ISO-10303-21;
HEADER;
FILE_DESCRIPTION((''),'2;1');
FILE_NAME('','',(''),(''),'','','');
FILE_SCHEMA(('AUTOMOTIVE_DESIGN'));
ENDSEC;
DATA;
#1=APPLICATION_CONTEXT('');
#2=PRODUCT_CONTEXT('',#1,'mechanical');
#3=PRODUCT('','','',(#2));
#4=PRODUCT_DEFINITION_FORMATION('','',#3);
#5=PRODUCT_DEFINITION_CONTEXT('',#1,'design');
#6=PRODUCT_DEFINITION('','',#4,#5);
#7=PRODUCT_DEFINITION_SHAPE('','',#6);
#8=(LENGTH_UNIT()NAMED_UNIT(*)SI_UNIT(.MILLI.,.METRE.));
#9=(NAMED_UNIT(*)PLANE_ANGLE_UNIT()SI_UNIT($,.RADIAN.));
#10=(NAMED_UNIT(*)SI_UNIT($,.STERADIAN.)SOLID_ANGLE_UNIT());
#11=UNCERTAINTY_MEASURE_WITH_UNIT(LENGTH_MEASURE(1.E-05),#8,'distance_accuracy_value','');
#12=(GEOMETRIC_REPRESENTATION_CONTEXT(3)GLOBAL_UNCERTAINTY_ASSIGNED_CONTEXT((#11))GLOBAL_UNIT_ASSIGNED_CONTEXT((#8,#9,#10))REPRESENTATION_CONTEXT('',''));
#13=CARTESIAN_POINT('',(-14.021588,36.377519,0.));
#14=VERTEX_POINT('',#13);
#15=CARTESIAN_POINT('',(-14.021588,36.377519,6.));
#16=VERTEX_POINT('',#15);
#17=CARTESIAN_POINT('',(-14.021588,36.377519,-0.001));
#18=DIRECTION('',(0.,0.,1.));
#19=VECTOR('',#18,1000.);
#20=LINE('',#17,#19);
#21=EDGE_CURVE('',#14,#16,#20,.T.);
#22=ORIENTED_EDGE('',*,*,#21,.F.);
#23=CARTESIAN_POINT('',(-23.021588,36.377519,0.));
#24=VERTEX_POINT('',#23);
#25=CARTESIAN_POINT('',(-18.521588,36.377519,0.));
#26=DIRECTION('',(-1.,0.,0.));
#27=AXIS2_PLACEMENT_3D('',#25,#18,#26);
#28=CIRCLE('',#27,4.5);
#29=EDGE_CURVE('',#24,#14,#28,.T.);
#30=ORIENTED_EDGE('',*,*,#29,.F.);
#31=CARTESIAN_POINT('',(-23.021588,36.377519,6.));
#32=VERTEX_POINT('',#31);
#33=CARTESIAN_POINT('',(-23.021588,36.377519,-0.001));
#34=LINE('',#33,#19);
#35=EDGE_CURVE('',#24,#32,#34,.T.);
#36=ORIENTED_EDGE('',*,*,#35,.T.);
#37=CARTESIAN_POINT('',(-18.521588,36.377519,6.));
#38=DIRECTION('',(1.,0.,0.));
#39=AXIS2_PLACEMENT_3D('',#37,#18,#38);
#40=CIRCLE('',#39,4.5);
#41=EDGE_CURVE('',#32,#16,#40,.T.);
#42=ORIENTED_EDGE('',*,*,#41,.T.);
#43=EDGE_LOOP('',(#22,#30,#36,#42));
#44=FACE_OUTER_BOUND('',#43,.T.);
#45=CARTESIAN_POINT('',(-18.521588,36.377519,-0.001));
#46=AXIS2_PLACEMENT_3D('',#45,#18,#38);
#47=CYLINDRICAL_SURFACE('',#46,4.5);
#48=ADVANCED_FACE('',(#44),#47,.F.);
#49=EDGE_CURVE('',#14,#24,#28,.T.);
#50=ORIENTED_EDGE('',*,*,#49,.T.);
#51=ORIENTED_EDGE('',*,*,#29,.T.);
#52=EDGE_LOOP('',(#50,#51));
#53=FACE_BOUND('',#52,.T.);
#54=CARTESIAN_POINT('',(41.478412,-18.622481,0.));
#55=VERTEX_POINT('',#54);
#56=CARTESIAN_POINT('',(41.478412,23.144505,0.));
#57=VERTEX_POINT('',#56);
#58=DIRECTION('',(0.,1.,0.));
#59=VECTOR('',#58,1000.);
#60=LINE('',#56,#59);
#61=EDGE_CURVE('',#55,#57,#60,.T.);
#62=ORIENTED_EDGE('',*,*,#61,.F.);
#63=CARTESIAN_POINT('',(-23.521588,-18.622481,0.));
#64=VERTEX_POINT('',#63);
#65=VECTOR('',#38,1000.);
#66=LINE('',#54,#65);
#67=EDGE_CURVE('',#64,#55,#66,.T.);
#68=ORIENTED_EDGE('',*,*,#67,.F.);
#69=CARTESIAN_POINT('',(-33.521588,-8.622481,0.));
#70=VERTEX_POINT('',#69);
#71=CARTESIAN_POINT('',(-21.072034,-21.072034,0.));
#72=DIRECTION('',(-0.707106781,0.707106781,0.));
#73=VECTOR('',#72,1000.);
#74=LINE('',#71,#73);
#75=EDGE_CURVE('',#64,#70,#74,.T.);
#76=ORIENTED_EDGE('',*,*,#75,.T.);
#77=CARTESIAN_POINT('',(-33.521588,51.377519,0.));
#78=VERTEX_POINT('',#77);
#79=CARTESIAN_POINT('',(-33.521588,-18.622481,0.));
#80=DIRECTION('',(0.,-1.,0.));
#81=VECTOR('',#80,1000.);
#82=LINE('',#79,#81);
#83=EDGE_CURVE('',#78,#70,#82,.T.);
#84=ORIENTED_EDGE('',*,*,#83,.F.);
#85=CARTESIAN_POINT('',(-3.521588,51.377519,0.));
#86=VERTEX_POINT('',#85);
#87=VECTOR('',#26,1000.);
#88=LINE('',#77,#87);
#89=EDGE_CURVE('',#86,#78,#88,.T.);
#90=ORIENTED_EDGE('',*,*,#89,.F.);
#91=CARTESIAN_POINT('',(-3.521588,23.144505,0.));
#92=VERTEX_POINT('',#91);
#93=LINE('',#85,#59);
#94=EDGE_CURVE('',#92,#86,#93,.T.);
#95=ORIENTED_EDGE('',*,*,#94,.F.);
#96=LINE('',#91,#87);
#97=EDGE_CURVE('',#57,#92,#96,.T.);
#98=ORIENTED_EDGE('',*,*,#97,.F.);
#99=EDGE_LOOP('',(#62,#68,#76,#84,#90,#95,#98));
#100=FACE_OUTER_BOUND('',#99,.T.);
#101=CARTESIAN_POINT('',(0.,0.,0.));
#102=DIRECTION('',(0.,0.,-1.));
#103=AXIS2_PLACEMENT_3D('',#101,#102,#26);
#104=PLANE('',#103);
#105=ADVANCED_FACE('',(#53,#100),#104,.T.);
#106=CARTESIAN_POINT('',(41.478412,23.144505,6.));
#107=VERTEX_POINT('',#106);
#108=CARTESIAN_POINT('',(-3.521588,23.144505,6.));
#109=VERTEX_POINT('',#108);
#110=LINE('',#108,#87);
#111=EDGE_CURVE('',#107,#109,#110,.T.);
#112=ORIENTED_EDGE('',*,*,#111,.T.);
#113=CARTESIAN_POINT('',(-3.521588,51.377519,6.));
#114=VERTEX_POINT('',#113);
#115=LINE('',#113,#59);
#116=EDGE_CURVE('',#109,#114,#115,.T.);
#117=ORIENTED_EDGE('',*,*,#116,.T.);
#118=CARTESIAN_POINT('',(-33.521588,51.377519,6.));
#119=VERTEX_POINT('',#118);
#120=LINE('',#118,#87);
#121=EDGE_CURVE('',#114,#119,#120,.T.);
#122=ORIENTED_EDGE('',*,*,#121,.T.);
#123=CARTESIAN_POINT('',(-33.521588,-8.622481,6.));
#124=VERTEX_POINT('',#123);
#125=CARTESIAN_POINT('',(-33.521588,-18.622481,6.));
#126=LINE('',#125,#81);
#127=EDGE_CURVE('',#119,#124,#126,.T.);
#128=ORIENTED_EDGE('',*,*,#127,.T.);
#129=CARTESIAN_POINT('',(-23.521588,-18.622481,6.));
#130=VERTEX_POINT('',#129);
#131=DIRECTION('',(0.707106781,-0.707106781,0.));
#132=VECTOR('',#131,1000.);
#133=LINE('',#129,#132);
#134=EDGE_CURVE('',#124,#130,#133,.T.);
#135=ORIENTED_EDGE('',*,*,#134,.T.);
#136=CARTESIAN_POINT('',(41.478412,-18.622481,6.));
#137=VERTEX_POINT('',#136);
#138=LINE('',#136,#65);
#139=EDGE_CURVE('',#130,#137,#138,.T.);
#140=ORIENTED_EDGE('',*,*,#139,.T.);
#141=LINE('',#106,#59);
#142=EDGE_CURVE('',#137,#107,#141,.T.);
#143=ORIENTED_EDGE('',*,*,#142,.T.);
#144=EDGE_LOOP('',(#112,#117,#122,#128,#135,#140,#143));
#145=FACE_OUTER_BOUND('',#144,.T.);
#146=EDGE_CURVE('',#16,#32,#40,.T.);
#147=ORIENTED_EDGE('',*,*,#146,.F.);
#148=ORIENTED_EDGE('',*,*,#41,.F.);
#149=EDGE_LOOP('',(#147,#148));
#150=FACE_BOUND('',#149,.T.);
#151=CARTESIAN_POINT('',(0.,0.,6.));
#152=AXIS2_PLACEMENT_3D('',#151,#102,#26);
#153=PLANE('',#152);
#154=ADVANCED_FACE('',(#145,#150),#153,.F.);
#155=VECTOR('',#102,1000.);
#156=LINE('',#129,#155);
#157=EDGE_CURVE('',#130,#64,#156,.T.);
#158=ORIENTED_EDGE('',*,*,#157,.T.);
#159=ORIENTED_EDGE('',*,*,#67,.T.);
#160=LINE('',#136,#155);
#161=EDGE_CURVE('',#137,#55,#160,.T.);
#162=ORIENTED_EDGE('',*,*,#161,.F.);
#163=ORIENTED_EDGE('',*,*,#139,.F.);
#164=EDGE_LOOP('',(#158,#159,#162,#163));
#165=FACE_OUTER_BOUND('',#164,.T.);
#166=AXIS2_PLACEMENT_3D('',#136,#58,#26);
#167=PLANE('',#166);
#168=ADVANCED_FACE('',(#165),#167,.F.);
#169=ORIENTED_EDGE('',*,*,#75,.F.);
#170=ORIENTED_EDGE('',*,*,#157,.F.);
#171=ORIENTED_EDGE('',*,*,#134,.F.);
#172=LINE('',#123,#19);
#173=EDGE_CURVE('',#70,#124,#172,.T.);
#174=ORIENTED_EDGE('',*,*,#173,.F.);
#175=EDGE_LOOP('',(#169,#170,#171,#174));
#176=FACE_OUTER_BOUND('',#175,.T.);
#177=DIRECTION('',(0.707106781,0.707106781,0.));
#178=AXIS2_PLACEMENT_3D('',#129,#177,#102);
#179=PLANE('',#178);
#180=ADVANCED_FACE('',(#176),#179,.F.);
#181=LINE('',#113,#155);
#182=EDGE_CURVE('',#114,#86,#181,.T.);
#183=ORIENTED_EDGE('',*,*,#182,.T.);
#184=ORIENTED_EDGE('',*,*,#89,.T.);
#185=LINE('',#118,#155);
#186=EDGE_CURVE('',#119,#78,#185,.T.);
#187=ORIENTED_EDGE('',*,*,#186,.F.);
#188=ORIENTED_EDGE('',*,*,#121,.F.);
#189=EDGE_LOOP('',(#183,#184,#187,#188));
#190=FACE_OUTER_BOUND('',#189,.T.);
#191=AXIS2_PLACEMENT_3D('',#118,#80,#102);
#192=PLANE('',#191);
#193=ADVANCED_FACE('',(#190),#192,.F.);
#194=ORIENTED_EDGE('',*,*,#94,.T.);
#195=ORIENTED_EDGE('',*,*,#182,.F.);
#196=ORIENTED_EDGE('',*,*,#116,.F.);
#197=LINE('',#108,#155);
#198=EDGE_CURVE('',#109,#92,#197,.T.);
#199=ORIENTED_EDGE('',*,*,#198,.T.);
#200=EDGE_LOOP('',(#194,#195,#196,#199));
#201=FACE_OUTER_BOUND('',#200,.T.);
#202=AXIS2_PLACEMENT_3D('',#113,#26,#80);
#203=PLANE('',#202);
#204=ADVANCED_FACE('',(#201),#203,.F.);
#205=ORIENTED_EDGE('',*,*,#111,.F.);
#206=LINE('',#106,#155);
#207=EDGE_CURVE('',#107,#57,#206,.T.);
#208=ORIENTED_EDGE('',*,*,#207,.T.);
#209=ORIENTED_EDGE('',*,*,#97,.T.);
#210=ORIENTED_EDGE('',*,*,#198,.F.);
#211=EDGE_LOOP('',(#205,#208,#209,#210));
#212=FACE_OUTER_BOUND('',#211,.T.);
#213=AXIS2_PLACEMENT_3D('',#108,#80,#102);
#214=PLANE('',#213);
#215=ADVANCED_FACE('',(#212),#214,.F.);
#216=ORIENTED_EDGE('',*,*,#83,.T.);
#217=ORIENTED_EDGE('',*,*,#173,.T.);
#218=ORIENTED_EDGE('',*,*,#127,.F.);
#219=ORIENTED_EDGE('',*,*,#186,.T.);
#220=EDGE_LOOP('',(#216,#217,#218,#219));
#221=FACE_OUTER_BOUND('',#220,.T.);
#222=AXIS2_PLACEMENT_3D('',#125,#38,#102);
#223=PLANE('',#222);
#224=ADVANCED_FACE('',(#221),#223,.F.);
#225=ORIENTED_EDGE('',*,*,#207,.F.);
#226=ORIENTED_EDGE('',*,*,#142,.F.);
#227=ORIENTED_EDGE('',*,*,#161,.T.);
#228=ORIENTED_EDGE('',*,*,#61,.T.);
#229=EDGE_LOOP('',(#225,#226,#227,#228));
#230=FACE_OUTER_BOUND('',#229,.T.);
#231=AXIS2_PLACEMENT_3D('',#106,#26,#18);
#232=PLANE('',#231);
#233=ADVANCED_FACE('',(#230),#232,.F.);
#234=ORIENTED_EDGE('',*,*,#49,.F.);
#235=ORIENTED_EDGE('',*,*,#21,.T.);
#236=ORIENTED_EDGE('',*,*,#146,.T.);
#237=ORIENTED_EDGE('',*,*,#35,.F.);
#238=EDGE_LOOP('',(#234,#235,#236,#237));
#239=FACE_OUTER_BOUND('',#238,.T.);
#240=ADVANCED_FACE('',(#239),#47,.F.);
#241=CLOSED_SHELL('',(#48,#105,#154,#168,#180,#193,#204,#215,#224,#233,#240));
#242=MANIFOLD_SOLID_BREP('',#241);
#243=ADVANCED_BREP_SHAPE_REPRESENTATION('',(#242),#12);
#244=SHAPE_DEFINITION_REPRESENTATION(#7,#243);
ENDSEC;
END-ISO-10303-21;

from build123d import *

# Parameters (mm, degrees)
BOSS_EXTRUDE1_DEPTH = 6
CUT_EXTRUDE1_REACH  = 68.303
SKETCH2_R           = 4.5
CHAMFER1_SIZE       = 10


with BuildPart() as part:
    # Sketch1 → Boss-Extrude1 (new body)
    with BuildSketch(Plane.XY):
        Polygon((-33.521587555, -18.6224812), (-33.521587555, 51.3775188), (-3.521587555, 51.3775188), (-3.521587555, 23.144505274), (41.478412445, 23.144505274), (41.478412445, -18.6224812), align=None)
    extrude(amount=BOSS_EXTRUDE1_DEPTH)

    # Sketch2 → Cut-Extrude1 (cut, up to next)
    with BuildSketch(Plane.XY.offset(6), mode=Mode.PRIVATE) as cut_extrude1_sk1:
        with Locations((-18.521587555, 36.3775188)):
            Circle(SKETCH2_R)
    cut_extrude1_tool1 = extrude(cut_extrude1_sk1.sketch, amount=-CUT_EXTRUDE1_REACH, mode=Mode.PRIVATE) & part.part
    add(cut_extrude1_tool1.solids().sort_by_distance((-18.521588, 36.377519, 6))[0], mode=Mode.SUBTRACT)

    # Chamfer1
    chamfer1_edges = [part.edges().sort_by_distance(p)[0] for p in [
        (-33.521587555, -18.6224812, 3),
    ]]
    chamfer(chamfer1_edges, length=CHAMFER1_SIZE)


solid = part.part
